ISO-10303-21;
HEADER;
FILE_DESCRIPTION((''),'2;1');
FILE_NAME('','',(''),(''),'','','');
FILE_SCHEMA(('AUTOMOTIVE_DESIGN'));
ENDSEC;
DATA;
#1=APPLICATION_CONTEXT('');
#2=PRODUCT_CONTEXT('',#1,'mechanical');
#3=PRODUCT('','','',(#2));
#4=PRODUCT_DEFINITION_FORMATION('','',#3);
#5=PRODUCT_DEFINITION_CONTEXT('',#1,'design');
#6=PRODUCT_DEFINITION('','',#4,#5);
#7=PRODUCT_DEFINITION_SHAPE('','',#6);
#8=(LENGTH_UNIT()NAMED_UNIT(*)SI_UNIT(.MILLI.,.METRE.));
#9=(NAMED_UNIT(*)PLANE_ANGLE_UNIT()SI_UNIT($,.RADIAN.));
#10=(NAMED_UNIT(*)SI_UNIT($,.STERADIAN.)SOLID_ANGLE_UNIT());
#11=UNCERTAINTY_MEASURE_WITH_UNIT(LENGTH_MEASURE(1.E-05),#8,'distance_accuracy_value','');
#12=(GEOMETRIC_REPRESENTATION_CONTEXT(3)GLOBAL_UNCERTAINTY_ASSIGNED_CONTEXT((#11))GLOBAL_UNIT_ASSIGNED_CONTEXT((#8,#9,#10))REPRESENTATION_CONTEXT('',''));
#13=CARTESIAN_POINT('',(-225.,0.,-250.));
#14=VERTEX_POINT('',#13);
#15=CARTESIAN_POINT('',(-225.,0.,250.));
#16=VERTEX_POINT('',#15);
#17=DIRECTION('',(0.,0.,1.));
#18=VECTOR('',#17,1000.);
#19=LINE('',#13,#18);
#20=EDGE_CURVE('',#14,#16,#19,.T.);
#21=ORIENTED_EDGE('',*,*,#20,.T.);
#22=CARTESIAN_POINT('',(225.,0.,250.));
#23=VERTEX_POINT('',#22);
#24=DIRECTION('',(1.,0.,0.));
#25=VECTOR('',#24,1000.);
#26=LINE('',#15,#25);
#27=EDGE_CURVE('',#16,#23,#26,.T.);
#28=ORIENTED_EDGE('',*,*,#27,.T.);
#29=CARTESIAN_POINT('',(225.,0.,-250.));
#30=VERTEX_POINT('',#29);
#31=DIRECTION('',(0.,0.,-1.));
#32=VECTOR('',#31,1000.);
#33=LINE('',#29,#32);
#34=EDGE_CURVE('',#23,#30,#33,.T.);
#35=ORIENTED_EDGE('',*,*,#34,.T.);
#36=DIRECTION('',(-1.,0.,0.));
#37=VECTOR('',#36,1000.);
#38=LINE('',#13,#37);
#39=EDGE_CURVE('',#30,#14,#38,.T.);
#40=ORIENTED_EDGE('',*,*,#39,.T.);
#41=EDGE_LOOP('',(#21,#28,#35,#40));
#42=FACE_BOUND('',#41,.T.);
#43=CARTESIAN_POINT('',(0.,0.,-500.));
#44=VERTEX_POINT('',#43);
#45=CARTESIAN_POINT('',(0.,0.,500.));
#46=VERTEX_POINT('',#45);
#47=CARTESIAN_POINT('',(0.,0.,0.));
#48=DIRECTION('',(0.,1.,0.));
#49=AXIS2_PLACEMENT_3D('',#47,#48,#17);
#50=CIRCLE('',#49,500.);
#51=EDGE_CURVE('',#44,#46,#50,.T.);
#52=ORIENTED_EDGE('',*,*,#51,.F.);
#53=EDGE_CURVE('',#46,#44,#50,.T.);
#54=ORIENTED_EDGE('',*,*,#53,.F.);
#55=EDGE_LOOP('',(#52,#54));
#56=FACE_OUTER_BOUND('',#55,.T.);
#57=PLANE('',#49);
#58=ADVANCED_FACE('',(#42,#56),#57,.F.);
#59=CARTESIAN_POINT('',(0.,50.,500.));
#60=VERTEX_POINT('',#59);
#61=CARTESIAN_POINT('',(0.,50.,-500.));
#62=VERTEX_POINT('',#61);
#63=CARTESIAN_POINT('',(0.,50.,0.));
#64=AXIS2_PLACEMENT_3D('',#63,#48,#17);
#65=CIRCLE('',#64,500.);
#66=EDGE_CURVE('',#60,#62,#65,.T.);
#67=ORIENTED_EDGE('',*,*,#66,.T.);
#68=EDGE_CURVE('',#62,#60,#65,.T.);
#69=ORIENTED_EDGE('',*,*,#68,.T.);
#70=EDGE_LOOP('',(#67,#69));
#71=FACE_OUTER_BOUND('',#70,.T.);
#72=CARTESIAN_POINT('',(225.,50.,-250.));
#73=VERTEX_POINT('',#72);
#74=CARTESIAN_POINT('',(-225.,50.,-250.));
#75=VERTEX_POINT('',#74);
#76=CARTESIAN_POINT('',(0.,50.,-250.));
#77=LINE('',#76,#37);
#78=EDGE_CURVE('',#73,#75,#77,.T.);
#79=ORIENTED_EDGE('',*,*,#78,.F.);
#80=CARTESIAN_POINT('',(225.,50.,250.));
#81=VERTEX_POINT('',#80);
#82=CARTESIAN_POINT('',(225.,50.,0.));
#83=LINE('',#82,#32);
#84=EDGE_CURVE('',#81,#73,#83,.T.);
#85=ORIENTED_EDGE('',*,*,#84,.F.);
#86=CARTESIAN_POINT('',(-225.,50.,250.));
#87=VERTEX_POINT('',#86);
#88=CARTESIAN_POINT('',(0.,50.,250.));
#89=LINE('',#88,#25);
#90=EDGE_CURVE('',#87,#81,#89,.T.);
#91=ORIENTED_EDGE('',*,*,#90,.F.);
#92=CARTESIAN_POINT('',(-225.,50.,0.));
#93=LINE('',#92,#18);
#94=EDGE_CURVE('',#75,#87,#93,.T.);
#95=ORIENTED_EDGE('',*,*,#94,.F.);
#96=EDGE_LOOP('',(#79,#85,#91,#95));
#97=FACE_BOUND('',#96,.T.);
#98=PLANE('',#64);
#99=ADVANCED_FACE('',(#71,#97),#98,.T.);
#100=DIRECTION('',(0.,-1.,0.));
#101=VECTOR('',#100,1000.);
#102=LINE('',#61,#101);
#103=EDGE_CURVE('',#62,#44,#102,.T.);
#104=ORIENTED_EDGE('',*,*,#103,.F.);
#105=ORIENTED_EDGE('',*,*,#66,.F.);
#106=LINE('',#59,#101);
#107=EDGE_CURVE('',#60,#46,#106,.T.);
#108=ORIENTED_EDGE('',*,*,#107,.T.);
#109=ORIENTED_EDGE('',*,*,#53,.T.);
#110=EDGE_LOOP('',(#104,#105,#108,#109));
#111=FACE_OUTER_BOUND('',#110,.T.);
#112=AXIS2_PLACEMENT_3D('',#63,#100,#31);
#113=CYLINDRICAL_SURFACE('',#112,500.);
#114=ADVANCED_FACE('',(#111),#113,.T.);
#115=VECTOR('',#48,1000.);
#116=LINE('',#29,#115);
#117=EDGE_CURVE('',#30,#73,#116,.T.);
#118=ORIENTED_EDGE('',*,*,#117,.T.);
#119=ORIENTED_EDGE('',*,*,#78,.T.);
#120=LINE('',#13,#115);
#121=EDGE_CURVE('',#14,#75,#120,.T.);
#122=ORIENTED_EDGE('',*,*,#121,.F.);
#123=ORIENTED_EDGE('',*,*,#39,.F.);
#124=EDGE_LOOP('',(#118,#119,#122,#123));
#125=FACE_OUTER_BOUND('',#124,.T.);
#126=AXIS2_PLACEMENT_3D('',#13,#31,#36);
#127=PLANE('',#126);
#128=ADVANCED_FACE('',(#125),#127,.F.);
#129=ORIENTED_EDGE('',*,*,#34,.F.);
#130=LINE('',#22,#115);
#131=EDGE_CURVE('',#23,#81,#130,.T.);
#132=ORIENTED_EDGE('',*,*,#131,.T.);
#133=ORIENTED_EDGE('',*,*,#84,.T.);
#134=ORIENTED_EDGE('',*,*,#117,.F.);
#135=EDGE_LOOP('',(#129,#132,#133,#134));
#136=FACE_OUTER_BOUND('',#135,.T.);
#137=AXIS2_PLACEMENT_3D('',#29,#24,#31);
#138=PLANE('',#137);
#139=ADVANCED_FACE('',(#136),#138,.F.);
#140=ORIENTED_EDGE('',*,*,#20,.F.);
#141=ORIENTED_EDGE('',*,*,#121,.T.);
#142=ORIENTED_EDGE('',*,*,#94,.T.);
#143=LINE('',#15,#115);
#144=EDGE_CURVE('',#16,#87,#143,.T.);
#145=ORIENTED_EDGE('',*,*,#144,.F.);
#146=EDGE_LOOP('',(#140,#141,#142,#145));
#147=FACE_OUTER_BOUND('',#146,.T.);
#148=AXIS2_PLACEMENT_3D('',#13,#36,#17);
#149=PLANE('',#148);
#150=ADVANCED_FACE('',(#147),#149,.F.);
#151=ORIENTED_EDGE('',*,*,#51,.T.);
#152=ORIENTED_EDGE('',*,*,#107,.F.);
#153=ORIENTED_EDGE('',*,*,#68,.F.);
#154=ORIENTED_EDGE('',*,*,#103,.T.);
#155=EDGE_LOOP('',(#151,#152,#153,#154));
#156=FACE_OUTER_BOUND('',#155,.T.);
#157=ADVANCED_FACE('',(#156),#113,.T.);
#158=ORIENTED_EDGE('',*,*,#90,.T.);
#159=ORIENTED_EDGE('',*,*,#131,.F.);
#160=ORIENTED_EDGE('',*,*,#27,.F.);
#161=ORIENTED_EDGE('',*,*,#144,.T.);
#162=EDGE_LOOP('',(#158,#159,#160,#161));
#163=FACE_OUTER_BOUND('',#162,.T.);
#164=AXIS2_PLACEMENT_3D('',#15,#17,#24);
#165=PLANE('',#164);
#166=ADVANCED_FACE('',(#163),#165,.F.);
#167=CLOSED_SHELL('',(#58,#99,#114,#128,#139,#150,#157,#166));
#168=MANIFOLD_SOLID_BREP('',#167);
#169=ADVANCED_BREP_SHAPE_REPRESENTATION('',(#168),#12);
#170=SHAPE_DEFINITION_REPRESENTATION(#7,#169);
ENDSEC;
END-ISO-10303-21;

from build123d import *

# Parameters (mm, degrees)
SKETCH1_R               = 500
BOSS_EXTRUDE1_DEPTH     = 50
CUT_EXTRUDE1_DEPTH      = 709.872343938
CUT_EXTRUDE1_DEPTH_BACK = 709.872343938
SKETCH2_W               = 450
SKETCH2_H               = 500


with BuildPart() as part:
    # Sketch1 → Boss-Extrude1 (new body)
    with BuildSketch(Plane(origin=(0, 0, 0), x_dir=(1, 0, 0), z_dir=(0, 1, 0))):
        with Locations(Location((0, 0, 0), (0, 0, 270))):
            Circle(SKETCH1_R)
    extrude(amount=BOSS_EXTRUDE1_DEPTH)

    # Sketch2 → Cut-Extrude1 (cut, two sides: drawn at the far end of the back side and taken through both)
    with BuildSketch(Plane(origin=(0, 50, 0), x_dir=(1, 0, 0), z_dir=(0, 1, 0)).offset(-CUT_EXTRUDE1_DEPTH_BACK)):
        Rectangle(SKETCH2_W, SKETCH2_H)
    extrude(amount=CUT_EXTRUDE1_DEPTH + CUT_EXTRUDE1_DEPTH_BACK, mode=Mode.SUBTRACT)


solid = part.part
